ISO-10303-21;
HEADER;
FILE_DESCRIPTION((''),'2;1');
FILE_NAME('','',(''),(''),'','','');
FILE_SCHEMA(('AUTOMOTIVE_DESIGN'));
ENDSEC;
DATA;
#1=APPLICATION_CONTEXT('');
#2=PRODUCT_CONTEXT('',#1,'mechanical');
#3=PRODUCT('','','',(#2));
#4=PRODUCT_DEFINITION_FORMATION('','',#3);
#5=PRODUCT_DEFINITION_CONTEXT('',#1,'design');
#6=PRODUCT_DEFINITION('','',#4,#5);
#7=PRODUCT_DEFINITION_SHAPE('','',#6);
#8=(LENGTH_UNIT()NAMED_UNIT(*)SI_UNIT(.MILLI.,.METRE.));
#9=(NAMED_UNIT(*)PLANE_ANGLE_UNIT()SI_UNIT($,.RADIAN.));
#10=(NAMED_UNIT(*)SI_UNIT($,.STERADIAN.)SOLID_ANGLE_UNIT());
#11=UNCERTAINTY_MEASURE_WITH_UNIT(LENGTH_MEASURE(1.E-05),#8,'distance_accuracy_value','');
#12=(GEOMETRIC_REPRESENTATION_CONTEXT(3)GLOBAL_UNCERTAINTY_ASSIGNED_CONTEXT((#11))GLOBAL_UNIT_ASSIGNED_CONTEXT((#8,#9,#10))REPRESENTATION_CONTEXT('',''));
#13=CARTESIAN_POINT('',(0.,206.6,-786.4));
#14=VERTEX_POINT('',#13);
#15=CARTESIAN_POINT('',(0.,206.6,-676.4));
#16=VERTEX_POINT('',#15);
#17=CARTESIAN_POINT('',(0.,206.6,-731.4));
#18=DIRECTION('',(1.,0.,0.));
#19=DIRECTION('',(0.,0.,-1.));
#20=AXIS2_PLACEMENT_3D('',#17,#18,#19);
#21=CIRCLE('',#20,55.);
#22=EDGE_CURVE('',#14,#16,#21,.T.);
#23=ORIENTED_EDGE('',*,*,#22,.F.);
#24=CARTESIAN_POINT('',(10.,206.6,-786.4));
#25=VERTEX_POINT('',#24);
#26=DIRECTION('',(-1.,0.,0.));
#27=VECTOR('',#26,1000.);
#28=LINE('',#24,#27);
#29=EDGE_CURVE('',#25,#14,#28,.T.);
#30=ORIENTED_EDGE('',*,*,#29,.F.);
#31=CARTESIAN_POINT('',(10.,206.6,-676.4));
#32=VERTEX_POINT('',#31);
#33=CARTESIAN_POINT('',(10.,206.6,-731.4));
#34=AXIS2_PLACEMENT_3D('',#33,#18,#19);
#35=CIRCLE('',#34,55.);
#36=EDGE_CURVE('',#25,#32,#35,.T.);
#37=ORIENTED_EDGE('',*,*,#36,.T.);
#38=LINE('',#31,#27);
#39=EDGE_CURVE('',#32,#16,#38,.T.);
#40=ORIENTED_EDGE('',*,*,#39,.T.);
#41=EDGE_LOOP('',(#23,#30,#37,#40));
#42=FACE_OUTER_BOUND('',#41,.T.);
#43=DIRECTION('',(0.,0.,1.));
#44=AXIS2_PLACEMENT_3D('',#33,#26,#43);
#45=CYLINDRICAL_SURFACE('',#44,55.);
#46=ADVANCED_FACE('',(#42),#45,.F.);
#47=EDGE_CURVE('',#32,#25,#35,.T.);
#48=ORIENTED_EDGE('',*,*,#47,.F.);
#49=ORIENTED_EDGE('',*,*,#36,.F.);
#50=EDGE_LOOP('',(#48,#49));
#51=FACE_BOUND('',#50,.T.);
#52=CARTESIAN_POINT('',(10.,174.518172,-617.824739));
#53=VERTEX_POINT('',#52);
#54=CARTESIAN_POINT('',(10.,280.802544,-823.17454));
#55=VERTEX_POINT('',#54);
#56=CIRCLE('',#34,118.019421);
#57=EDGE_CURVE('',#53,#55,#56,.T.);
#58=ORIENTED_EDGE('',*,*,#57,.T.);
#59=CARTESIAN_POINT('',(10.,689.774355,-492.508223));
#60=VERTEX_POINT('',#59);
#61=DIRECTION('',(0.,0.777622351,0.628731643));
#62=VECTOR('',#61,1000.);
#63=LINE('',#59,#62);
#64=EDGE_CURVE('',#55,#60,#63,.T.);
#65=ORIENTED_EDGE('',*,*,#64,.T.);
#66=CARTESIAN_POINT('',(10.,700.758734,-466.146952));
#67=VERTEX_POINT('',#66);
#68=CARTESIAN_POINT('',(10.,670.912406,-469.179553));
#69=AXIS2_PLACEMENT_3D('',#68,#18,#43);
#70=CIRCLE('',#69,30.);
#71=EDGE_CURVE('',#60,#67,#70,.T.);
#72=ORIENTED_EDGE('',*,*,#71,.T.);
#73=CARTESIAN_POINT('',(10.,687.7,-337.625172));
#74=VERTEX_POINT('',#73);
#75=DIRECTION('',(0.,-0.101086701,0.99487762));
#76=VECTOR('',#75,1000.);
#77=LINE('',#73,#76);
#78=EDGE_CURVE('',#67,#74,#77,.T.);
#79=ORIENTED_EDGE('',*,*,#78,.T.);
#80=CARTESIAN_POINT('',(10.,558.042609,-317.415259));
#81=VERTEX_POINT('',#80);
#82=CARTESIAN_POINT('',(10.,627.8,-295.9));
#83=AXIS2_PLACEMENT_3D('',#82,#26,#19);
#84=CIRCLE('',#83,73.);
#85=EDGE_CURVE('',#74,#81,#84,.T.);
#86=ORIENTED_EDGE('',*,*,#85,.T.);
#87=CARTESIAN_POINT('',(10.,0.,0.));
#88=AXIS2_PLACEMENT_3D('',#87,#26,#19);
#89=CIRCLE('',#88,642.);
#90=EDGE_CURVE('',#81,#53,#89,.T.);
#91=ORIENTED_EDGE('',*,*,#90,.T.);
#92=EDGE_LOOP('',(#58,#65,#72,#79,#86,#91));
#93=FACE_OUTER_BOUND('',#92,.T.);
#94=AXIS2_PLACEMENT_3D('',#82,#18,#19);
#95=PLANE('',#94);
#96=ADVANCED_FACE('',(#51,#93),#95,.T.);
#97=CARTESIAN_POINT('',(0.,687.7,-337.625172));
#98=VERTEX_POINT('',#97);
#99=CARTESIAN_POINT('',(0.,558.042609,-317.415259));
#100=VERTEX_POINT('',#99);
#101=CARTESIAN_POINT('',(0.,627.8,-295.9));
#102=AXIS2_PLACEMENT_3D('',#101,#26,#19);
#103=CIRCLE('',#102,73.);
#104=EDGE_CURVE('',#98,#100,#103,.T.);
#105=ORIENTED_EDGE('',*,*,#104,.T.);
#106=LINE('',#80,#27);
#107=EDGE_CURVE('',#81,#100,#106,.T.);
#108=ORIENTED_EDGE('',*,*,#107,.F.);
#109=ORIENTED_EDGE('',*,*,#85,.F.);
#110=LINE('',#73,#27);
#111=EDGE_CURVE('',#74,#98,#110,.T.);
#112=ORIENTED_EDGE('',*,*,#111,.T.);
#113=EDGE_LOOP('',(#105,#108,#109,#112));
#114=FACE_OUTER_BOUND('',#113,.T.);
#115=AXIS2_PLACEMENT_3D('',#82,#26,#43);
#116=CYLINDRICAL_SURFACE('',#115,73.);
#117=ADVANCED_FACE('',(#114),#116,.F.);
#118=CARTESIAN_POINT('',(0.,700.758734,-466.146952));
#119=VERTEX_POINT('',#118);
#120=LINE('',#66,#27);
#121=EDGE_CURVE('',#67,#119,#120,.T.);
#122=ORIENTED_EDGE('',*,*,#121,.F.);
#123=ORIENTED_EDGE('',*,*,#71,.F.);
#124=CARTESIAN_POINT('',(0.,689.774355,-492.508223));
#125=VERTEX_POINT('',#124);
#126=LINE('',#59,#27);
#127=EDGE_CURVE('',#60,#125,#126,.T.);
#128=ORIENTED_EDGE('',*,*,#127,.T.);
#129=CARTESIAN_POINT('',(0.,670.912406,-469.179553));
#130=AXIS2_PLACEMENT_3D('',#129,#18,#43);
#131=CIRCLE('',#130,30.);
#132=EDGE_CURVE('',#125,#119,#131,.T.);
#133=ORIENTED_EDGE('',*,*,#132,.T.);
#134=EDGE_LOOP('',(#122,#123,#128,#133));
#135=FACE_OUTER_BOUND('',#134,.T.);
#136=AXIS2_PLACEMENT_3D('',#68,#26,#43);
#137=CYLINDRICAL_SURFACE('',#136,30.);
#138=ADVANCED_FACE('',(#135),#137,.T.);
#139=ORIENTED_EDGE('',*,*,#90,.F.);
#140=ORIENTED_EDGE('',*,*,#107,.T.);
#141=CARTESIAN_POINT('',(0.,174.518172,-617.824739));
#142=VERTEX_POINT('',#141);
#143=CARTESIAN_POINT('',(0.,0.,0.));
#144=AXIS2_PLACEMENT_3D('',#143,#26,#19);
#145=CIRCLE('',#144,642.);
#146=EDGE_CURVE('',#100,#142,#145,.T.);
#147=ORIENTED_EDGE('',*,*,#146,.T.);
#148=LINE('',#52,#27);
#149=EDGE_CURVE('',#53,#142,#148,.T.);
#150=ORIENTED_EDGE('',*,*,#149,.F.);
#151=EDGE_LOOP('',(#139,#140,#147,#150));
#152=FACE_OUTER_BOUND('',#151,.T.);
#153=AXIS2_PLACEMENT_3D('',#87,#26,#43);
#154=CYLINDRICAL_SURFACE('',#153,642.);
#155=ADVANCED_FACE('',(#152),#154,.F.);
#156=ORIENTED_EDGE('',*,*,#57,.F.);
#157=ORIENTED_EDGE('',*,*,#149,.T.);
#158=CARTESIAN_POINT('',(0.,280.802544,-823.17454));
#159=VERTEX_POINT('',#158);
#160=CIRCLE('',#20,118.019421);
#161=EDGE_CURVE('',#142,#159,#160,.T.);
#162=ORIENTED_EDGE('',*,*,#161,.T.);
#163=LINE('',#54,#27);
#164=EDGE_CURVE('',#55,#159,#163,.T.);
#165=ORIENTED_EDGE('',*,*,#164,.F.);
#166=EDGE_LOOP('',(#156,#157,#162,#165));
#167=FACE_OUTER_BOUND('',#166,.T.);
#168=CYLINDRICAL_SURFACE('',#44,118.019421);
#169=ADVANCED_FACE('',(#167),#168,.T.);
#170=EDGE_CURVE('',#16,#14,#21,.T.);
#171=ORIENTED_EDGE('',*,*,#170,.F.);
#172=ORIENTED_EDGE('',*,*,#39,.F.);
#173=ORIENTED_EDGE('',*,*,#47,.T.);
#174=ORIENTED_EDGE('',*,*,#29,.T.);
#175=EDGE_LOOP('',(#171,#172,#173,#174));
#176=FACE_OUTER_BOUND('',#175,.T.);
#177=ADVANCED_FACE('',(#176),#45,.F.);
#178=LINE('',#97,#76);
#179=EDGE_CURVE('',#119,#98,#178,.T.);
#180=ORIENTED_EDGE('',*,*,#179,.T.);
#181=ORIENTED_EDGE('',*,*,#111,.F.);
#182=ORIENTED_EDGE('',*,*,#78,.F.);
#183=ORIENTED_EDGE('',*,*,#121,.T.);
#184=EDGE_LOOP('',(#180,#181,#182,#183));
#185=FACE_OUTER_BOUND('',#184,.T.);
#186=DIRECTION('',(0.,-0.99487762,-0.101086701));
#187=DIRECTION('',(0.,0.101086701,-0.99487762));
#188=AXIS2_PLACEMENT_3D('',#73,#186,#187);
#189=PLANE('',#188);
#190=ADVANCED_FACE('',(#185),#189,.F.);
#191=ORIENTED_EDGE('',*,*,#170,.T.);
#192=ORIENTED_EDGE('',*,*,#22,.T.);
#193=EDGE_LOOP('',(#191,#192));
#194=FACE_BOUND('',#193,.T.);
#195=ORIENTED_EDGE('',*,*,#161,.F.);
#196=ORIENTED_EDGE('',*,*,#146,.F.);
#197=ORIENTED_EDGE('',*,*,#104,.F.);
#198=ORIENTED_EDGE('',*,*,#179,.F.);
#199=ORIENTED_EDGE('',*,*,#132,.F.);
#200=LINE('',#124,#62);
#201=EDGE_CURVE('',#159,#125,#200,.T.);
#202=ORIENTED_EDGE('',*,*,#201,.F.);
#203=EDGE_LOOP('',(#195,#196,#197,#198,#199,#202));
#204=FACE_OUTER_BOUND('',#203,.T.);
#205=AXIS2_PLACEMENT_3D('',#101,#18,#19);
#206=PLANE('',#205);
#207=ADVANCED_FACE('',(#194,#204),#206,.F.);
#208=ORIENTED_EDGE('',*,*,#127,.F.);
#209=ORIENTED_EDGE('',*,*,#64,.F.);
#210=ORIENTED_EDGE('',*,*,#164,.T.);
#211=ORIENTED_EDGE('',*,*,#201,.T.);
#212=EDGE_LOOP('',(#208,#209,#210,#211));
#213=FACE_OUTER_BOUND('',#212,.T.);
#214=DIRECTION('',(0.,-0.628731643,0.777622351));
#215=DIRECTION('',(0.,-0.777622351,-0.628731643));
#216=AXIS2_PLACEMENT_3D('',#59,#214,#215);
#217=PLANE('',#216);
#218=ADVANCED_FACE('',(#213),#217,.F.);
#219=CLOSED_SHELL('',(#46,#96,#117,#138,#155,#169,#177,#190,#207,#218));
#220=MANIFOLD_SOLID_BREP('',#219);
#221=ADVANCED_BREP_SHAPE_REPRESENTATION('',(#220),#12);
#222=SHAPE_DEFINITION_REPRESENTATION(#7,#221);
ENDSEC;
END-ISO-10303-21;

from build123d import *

# Parameters (mm, degrees)
SKETCH1_R           = 55
BOSS_EXTRUDE1_DEPTH = 10


with BuildPart() as part:
    # Sketch1 → Boss-Extrude1 (new body)
    with BuildSketch(Plane(origin=(0, 0, 0), x_dir=(0, 0, -1), z_dir=(1, 0, 0))):
        with BuildLine():
            Line((337.625172258, 687.7), (466.146951534, 700.758734438))
            ThreePointArc((466.146951534, 700.758734438), (480.718476107, 698.604521018), (492.508223096, 689.774355121))
            Line((492.508223096, 689.774355121), (823.174539509, 280.80254433))
            ThreePointArc((823.174539509, 280.80254433), (785.648592785, 101.78743459), (617.824738614, 174.518171996))
            ThreePointArc((617.824738614, 174.518171996), (505.411922854, 395.882290886), (317.415259146, 558.042608823))
            ThreePointArc((317.415259146, 558.042608823), (368.029035851, 616.55712727), (337.625172258, 687.7))
        make_face()
        with Locations((731.4, 206.6)):
            Circle(SKETCH1_R, mode=Mode.SUBTRACT)
    extrude(amount=BOSS_EXTRUDE1_DEPTH)


solid = part.part
